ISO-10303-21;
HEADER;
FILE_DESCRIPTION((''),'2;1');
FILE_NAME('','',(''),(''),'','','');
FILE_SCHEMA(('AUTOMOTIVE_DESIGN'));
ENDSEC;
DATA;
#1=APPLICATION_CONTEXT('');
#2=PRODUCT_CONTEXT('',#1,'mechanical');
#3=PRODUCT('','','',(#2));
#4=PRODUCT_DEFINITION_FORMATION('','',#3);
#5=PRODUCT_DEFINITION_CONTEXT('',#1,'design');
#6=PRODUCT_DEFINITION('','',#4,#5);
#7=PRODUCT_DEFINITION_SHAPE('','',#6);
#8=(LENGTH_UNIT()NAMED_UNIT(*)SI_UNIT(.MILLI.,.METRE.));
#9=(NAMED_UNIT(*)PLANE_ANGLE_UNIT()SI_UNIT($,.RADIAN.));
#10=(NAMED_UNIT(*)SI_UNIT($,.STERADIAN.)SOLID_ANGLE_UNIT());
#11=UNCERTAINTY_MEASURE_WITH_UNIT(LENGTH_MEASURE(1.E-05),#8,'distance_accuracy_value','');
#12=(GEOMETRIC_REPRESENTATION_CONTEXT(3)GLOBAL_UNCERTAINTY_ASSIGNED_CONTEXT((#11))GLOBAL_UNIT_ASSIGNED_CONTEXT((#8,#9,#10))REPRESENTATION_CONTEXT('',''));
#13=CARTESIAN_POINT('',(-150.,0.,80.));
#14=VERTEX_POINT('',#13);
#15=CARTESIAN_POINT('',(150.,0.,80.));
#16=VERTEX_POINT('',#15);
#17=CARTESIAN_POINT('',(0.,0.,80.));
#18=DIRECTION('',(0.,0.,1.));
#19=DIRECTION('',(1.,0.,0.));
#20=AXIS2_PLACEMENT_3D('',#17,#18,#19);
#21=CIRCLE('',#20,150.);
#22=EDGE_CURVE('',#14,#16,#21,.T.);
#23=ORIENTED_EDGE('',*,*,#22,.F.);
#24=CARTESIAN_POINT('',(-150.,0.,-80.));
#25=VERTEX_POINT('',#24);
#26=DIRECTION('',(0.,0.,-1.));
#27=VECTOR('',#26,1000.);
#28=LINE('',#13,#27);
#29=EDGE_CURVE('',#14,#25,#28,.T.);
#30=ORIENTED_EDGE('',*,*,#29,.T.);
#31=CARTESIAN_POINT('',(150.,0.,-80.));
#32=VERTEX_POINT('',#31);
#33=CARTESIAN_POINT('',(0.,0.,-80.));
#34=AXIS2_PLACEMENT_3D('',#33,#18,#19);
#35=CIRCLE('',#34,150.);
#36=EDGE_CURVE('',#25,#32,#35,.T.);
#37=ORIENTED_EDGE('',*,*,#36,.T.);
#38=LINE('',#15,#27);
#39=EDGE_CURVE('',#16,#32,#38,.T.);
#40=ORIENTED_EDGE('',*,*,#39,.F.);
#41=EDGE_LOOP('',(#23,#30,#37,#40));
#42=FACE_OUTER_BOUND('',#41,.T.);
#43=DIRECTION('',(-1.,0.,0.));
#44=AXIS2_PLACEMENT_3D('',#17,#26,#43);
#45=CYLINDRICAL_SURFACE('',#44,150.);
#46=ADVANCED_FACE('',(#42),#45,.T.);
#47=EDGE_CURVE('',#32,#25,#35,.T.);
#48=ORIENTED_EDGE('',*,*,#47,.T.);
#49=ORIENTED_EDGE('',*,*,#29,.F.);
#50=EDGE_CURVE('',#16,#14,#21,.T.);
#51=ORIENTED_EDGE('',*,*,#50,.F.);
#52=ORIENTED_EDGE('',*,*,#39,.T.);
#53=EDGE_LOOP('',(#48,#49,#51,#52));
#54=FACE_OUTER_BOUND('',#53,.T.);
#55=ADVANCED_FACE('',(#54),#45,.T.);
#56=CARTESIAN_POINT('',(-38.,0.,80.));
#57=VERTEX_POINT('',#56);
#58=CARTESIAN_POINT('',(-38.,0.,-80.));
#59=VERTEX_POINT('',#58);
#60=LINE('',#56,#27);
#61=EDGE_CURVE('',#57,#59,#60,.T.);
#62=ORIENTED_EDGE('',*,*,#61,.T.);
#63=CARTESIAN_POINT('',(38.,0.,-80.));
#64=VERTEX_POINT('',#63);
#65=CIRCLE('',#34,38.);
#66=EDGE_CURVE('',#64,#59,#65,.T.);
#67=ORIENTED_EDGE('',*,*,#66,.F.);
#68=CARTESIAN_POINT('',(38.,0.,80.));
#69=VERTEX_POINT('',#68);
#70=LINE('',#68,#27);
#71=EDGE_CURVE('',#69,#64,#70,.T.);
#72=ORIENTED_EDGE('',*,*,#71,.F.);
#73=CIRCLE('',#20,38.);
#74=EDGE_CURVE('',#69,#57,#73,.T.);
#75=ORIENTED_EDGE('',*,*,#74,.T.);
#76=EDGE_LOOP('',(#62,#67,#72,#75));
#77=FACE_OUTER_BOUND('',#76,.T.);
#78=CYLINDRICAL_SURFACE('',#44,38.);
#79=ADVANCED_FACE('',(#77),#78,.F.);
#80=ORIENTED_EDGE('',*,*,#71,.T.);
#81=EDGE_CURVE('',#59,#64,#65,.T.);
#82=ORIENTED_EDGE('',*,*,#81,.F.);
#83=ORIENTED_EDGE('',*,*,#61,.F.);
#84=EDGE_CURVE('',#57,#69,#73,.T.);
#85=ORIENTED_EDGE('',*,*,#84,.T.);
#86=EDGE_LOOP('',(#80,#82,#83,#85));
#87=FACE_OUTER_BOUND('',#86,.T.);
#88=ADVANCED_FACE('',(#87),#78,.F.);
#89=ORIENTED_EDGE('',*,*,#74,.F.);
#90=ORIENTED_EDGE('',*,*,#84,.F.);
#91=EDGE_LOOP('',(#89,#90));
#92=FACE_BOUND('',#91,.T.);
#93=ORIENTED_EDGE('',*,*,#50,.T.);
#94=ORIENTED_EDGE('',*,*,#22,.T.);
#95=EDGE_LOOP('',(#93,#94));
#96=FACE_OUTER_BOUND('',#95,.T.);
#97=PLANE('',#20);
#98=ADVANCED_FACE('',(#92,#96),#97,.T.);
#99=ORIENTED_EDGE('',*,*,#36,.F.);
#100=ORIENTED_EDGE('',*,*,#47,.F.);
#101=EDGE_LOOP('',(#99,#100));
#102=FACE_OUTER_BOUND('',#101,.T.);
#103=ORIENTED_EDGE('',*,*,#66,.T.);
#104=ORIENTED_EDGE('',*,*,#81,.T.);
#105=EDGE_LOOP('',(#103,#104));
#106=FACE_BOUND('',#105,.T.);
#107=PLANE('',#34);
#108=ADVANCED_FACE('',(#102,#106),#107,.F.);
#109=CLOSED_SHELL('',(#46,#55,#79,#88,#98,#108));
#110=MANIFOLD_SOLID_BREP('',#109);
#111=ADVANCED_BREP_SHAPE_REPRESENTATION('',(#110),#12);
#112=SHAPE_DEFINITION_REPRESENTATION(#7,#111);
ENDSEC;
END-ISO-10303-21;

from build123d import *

# Parameters (mm, degrees)
SKETCH_1_R      = 150
SKETCH_1_R_2    = 38
EXTRUDE_1_DEPTH = 80


with BuildPart() as part:
    # 草图1 → 凸台-拉伸1 (new, symmetric)
    with BuildSketch(Plane.XY):
        Circle(SKETCH_1_R)
        Circle(SKETCH_1_R_2, mode=Mode.SUBTRACT)
    extrude(amount=EXTRUDE_1_DEPTH, both=True)


solid = part.part
